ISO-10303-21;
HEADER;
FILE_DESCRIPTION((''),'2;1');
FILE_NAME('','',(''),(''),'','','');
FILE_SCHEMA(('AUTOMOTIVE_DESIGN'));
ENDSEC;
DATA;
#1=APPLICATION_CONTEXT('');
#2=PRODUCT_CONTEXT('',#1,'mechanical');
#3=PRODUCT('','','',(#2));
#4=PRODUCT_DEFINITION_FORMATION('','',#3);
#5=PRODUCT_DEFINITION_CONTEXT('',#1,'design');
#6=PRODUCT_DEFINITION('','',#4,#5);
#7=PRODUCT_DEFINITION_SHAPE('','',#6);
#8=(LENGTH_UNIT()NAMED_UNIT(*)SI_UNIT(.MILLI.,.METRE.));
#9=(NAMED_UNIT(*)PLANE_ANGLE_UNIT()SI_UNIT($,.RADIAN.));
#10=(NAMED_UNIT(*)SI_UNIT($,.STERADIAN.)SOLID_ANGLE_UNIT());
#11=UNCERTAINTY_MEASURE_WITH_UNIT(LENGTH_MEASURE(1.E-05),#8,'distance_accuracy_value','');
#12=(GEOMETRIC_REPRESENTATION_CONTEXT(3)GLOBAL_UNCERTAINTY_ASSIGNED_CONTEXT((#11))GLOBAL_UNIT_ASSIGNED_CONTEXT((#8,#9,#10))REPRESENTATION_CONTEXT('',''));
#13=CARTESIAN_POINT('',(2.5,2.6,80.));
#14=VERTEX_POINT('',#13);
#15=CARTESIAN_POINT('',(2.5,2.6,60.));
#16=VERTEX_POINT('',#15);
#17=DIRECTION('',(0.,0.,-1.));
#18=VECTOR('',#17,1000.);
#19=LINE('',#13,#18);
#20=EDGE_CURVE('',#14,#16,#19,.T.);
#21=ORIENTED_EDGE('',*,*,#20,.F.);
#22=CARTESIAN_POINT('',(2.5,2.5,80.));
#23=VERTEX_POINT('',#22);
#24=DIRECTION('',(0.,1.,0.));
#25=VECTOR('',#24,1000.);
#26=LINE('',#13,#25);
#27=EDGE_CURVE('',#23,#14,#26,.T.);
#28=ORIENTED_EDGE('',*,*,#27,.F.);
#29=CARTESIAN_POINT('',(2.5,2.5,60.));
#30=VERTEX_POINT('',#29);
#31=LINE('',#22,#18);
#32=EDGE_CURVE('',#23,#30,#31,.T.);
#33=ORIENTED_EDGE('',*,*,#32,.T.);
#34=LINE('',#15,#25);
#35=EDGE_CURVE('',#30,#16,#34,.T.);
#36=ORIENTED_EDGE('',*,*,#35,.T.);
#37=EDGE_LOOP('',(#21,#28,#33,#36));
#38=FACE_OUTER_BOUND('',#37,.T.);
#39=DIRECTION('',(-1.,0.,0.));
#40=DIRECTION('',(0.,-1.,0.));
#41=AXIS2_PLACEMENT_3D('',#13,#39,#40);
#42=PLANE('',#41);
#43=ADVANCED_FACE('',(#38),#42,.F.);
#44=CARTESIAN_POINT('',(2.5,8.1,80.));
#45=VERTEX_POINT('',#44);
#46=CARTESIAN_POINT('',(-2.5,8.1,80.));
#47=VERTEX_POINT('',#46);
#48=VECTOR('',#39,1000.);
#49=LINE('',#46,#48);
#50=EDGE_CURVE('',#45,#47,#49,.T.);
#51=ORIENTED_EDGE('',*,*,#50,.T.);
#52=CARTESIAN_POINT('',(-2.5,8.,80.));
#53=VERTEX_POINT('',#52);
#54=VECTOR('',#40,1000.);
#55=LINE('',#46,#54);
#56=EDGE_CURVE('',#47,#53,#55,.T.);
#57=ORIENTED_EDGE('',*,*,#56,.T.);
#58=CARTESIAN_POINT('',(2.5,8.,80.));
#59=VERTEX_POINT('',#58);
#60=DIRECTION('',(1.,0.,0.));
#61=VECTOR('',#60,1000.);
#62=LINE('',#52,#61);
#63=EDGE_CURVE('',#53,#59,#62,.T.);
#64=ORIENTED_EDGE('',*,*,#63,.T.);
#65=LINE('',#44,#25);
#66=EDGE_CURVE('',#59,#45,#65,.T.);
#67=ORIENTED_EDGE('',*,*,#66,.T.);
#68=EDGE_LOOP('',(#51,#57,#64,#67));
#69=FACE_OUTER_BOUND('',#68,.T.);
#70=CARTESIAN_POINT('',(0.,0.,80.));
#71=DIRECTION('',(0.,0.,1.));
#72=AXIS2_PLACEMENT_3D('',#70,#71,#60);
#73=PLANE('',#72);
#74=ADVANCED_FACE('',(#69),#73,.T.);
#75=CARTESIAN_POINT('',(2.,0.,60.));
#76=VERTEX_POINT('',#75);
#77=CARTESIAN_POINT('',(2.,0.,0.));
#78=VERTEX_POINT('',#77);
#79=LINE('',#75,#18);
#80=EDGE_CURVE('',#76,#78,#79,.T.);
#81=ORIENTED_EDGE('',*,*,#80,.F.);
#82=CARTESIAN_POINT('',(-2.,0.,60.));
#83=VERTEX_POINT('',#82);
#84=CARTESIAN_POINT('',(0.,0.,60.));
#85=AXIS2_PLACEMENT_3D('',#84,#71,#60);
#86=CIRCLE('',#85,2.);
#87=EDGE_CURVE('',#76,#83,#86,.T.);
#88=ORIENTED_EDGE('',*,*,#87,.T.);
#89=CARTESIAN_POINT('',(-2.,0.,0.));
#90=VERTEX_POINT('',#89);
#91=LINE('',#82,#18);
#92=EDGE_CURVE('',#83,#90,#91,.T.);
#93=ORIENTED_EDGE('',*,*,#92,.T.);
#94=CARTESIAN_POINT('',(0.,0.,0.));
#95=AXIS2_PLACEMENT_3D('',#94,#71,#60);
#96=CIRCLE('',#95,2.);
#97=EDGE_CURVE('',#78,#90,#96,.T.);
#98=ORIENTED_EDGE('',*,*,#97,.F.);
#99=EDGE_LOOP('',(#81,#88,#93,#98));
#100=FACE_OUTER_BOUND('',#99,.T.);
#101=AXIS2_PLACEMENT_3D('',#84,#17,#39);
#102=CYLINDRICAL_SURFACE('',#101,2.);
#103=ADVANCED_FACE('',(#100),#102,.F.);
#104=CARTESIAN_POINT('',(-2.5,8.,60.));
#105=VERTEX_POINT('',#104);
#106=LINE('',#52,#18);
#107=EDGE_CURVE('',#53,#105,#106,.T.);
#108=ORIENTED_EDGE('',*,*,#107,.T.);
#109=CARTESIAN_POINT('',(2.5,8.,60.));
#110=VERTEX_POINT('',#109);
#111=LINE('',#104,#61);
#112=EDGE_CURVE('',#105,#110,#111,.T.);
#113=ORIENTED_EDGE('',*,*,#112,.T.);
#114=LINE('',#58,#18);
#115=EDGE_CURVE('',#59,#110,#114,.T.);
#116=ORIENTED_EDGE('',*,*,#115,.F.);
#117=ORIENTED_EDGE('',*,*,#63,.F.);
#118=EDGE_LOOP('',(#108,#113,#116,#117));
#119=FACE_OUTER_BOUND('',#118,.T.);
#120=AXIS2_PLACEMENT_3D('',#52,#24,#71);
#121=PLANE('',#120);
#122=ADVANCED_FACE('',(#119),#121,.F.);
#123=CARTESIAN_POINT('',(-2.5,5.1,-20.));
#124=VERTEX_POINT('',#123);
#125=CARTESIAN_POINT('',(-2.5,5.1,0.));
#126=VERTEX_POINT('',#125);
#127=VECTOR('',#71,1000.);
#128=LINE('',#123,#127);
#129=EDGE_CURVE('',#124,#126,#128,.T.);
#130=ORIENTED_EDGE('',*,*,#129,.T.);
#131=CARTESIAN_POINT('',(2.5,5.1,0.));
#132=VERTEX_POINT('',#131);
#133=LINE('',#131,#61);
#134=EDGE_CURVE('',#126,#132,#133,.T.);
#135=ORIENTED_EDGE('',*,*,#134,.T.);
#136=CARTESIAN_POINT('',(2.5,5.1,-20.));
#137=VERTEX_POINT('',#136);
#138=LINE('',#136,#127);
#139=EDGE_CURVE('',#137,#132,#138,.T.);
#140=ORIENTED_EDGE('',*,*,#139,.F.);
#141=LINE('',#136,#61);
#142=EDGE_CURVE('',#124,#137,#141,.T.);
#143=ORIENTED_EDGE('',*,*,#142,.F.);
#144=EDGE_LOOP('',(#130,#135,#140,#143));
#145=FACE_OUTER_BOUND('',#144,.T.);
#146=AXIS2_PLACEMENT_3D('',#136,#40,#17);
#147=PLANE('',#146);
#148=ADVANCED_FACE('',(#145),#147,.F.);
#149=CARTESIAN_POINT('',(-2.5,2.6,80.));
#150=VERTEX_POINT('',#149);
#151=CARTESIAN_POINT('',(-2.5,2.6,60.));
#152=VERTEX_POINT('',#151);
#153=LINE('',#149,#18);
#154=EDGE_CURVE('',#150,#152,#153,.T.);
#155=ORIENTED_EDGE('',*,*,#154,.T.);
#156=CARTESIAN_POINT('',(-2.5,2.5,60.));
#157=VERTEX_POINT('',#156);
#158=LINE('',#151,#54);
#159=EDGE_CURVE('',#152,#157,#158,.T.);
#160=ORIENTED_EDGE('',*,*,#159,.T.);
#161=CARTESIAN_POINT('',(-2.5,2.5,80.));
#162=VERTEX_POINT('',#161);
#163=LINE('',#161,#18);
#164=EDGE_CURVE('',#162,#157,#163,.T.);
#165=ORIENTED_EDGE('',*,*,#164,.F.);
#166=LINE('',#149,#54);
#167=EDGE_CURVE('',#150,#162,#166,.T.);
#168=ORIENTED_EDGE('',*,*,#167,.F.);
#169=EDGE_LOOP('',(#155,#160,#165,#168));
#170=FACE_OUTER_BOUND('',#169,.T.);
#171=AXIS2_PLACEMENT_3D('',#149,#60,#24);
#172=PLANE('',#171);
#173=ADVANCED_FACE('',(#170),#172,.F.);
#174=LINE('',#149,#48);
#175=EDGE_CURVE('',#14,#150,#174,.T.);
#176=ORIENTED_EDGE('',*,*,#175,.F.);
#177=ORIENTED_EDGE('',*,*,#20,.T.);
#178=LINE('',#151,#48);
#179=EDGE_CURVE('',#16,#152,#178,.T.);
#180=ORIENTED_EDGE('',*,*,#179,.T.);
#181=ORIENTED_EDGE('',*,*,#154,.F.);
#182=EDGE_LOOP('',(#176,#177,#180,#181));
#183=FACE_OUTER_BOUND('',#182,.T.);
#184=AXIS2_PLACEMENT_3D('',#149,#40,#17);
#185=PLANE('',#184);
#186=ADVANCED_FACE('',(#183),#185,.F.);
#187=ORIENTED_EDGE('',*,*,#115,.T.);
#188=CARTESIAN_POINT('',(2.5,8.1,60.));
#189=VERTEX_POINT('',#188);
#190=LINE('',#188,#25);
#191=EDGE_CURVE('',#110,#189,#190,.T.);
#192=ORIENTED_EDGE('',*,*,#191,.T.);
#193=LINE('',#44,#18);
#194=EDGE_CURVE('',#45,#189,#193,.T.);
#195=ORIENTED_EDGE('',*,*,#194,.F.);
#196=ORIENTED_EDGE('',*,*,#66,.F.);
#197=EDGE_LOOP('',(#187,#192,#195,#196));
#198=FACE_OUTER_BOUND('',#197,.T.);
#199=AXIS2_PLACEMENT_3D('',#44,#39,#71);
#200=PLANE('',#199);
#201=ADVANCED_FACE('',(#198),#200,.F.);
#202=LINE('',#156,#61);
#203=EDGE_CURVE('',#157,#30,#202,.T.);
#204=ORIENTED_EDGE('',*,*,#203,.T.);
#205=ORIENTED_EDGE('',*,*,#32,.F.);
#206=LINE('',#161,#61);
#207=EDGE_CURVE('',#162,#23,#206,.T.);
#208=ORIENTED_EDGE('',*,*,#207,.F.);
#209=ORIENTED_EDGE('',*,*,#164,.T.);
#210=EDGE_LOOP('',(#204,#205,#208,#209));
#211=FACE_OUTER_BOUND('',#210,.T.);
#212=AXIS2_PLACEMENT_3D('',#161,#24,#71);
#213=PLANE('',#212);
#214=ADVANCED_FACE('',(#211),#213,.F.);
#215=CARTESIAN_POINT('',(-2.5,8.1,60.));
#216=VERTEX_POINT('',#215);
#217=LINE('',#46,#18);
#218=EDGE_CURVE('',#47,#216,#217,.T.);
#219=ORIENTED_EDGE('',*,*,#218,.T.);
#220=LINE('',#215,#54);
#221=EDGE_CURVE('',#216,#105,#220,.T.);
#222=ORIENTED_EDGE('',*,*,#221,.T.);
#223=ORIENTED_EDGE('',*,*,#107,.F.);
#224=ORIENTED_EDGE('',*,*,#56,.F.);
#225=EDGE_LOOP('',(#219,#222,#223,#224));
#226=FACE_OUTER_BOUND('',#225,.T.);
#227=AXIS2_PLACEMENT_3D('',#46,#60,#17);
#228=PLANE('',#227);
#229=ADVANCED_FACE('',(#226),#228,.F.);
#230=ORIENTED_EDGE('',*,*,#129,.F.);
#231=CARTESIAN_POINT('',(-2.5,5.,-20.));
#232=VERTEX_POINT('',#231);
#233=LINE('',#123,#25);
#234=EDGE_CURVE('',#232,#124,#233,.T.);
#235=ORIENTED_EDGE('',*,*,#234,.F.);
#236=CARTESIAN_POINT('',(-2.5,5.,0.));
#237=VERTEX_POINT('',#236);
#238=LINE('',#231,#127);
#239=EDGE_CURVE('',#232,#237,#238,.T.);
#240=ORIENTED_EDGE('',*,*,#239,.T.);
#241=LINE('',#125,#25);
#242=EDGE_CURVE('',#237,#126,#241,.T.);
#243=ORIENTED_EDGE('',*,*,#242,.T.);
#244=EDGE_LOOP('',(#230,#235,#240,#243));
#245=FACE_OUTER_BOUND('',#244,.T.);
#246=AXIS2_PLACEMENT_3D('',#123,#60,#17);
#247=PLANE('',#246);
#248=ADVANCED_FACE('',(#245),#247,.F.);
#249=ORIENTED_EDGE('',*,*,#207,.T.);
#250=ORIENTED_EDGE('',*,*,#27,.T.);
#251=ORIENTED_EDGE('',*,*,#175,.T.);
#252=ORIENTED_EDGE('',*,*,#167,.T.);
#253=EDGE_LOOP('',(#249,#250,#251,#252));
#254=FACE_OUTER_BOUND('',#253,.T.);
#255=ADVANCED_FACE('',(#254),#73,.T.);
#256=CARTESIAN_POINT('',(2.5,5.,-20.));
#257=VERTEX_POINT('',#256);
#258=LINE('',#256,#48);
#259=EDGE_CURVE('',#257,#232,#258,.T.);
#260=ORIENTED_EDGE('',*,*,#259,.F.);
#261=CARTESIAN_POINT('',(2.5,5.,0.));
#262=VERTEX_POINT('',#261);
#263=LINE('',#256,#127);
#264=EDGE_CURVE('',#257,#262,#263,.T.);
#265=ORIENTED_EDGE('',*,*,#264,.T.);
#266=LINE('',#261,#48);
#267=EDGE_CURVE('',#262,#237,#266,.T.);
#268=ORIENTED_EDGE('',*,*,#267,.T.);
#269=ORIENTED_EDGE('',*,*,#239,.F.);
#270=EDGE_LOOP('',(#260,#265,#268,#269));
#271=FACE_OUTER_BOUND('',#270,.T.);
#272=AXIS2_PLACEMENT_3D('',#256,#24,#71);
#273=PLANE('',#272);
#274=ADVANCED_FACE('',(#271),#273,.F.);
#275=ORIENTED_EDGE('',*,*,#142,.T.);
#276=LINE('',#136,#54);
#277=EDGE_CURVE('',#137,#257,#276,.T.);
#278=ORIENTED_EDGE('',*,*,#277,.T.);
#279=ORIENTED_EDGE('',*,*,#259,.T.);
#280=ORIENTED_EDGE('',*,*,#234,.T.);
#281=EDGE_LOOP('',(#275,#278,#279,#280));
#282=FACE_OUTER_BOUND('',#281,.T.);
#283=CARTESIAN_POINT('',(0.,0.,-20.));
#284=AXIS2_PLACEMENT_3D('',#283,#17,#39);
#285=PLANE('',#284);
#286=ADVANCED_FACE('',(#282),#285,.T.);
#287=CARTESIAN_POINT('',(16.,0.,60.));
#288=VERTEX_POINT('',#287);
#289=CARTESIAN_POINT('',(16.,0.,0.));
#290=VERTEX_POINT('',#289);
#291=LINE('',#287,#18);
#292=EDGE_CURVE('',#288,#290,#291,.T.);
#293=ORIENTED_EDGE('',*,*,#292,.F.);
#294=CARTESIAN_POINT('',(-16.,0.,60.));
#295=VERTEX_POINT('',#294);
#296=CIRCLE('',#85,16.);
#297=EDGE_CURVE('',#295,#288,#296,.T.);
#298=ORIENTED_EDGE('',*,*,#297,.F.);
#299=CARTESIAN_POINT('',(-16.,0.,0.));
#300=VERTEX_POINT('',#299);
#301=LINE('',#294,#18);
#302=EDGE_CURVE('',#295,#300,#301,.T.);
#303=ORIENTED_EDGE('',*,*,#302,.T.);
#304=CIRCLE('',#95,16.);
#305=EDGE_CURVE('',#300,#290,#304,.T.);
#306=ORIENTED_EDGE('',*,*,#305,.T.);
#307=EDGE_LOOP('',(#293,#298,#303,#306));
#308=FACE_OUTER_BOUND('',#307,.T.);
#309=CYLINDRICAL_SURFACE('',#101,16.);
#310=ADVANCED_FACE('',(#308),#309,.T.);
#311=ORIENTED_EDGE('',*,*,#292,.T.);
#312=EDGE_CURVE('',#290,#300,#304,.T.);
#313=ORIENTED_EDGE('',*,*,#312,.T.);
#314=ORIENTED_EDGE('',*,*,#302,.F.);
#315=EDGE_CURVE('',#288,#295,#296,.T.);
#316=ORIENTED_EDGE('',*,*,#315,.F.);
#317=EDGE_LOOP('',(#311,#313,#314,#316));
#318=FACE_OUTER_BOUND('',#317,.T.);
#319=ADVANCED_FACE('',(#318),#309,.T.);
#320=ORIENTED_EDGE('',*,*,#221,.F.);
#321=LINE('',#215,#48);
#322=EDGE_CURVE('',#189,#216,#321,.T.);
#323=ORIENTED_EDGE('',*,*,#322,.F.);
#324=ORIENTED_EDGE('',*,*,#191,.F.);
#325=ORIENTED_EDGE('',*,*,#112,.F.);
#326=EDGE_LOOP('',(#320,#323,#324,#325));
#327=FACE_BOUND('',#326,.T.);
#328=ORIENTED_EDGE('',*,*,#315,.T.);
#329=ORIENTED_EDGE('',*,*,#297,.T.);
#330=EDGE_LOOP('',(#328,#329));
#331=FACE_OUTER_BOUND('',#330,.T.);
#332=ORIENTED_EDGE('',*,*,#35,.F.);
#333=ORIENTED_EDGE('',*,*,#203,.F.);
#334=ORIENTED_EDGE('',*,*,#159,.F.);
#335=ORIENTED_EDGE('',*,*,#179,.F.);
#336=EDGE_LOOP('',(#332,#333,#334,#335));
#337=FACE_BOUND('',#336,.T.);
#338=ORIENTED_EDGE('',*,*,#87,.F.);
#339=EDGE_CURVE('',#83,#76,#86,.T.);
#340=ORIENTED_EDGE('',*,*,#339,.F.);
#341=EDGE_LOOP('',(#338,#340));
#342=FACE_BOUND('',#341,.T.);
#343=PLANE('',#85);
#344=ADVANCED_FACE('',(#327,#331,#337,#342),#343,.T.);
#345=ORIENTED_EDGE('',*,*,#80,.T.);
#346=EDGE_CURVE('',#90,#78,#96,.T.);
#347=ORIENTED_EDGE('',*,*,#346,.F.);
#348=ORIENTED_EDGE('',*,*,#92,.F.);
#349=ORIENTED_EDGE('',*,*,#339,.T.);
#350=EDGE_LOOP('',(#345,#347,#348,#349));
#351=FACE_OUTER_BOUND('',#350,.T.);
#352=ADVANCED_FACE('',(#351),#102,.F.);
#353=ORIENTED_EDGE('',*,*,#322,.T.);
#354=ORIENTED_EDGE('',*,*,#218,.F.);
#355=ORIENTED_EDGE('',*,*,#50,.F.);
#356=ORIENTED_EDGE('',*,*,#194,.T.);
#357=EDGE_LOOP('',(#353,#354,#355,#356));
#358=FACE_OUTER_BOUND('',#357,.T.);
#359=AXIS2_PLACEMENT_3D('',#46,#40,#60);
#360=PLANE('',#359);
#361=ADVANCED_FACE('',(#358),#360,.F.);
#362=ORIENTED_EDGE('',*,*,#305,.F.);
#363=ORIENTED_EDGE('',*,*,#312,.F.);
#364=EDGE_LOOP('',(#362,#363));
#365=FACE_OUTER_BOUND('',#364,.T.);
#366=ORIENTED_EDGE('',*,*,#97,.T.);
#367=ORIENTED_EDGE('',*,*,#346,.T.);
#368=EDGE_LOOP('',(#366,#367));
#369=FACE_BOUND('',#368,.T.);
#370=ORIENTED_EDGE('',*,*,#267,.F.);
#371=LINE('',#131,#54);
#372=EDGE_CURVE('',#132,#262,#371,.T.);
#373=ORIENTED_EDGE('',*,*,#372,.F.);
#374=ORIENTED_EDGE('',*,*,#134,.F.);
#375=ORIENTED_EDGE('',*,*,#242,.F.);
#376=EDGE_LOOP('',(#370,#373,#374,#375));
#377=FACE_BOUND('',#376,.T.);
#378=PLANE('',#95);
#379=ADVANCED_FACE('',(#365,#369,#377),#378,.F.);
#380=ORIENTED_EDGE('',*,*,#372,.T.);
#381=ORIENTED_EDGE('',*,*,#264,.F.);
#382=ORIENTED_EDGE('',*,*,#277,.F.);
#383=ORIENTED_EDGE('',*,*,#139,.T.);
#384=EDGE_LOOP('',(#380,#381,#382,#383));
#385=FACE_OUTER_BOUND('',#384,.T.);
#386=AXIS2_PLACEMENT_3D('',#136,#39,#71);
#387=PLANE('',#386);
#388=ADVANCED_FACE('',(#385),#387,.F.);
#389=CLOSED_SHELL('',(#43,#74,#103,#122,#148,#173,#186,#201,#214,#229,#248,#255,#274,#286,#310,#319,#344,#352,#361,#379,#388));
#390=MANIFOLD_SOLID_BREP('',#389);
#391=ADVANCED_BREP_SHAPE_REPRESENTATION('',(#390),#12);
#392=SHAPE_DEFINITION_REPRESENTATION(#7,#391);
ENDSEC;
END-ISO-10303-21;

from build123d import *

# Parameters (mm, degrees)
SKETCH1_R           = 16
SKETCH1_R_2         = 2
BOSS_EXTRUDE1_DEPTH = 60
SKETCH2_W           = 5
SKETCH2_H           = 0.1
BOSS_EXTRUDE2_DEPTH = 20
SKETCH3_W           = 5
SKETCH3_H           = 0.1
BOSS_EXTRUDE3_DEPTH = 20


with BuildPart() as part:
    # Sketch1 → Boss-Extrude1 (new body)
    with BuildSketch(Plane.XY):
        Circle(SKETCH1_R)
        Circle(SKETCH1_R_2, mode=Mode.SUBTRACT)
    extrude(amount=BOSS_EXTRUDE1_DEPTH)

    # Sketch2 → Boss-Extrude2 (add)
    with BuildSketch(Plane(origin=(0, 0, 0), x_dir=(-1, 0, 0), z_dir=(0, 0, -1))):
        with Locations((0, 5.05)):
            Rectangle(SKETCH2_W, SKETCH2_H)
    extrude(amount=BOSS_EXTRUDE2_DEPTH)

    # Sketch3 → Boss-Extrude3 (add)
    with BuildSketch(Plane.XY.offset(60)):
        with Locations((0, 8.05)):
            Rectangle(SKETCH3_W, SKETCH3_H)
        with Locations((0, 2.55)):
            Rectangle(SKETCH3_W, SKETCH3_H)
    extrude(amount=BOSS_EXTRUDE3_DEPTH)


solid = part.part
